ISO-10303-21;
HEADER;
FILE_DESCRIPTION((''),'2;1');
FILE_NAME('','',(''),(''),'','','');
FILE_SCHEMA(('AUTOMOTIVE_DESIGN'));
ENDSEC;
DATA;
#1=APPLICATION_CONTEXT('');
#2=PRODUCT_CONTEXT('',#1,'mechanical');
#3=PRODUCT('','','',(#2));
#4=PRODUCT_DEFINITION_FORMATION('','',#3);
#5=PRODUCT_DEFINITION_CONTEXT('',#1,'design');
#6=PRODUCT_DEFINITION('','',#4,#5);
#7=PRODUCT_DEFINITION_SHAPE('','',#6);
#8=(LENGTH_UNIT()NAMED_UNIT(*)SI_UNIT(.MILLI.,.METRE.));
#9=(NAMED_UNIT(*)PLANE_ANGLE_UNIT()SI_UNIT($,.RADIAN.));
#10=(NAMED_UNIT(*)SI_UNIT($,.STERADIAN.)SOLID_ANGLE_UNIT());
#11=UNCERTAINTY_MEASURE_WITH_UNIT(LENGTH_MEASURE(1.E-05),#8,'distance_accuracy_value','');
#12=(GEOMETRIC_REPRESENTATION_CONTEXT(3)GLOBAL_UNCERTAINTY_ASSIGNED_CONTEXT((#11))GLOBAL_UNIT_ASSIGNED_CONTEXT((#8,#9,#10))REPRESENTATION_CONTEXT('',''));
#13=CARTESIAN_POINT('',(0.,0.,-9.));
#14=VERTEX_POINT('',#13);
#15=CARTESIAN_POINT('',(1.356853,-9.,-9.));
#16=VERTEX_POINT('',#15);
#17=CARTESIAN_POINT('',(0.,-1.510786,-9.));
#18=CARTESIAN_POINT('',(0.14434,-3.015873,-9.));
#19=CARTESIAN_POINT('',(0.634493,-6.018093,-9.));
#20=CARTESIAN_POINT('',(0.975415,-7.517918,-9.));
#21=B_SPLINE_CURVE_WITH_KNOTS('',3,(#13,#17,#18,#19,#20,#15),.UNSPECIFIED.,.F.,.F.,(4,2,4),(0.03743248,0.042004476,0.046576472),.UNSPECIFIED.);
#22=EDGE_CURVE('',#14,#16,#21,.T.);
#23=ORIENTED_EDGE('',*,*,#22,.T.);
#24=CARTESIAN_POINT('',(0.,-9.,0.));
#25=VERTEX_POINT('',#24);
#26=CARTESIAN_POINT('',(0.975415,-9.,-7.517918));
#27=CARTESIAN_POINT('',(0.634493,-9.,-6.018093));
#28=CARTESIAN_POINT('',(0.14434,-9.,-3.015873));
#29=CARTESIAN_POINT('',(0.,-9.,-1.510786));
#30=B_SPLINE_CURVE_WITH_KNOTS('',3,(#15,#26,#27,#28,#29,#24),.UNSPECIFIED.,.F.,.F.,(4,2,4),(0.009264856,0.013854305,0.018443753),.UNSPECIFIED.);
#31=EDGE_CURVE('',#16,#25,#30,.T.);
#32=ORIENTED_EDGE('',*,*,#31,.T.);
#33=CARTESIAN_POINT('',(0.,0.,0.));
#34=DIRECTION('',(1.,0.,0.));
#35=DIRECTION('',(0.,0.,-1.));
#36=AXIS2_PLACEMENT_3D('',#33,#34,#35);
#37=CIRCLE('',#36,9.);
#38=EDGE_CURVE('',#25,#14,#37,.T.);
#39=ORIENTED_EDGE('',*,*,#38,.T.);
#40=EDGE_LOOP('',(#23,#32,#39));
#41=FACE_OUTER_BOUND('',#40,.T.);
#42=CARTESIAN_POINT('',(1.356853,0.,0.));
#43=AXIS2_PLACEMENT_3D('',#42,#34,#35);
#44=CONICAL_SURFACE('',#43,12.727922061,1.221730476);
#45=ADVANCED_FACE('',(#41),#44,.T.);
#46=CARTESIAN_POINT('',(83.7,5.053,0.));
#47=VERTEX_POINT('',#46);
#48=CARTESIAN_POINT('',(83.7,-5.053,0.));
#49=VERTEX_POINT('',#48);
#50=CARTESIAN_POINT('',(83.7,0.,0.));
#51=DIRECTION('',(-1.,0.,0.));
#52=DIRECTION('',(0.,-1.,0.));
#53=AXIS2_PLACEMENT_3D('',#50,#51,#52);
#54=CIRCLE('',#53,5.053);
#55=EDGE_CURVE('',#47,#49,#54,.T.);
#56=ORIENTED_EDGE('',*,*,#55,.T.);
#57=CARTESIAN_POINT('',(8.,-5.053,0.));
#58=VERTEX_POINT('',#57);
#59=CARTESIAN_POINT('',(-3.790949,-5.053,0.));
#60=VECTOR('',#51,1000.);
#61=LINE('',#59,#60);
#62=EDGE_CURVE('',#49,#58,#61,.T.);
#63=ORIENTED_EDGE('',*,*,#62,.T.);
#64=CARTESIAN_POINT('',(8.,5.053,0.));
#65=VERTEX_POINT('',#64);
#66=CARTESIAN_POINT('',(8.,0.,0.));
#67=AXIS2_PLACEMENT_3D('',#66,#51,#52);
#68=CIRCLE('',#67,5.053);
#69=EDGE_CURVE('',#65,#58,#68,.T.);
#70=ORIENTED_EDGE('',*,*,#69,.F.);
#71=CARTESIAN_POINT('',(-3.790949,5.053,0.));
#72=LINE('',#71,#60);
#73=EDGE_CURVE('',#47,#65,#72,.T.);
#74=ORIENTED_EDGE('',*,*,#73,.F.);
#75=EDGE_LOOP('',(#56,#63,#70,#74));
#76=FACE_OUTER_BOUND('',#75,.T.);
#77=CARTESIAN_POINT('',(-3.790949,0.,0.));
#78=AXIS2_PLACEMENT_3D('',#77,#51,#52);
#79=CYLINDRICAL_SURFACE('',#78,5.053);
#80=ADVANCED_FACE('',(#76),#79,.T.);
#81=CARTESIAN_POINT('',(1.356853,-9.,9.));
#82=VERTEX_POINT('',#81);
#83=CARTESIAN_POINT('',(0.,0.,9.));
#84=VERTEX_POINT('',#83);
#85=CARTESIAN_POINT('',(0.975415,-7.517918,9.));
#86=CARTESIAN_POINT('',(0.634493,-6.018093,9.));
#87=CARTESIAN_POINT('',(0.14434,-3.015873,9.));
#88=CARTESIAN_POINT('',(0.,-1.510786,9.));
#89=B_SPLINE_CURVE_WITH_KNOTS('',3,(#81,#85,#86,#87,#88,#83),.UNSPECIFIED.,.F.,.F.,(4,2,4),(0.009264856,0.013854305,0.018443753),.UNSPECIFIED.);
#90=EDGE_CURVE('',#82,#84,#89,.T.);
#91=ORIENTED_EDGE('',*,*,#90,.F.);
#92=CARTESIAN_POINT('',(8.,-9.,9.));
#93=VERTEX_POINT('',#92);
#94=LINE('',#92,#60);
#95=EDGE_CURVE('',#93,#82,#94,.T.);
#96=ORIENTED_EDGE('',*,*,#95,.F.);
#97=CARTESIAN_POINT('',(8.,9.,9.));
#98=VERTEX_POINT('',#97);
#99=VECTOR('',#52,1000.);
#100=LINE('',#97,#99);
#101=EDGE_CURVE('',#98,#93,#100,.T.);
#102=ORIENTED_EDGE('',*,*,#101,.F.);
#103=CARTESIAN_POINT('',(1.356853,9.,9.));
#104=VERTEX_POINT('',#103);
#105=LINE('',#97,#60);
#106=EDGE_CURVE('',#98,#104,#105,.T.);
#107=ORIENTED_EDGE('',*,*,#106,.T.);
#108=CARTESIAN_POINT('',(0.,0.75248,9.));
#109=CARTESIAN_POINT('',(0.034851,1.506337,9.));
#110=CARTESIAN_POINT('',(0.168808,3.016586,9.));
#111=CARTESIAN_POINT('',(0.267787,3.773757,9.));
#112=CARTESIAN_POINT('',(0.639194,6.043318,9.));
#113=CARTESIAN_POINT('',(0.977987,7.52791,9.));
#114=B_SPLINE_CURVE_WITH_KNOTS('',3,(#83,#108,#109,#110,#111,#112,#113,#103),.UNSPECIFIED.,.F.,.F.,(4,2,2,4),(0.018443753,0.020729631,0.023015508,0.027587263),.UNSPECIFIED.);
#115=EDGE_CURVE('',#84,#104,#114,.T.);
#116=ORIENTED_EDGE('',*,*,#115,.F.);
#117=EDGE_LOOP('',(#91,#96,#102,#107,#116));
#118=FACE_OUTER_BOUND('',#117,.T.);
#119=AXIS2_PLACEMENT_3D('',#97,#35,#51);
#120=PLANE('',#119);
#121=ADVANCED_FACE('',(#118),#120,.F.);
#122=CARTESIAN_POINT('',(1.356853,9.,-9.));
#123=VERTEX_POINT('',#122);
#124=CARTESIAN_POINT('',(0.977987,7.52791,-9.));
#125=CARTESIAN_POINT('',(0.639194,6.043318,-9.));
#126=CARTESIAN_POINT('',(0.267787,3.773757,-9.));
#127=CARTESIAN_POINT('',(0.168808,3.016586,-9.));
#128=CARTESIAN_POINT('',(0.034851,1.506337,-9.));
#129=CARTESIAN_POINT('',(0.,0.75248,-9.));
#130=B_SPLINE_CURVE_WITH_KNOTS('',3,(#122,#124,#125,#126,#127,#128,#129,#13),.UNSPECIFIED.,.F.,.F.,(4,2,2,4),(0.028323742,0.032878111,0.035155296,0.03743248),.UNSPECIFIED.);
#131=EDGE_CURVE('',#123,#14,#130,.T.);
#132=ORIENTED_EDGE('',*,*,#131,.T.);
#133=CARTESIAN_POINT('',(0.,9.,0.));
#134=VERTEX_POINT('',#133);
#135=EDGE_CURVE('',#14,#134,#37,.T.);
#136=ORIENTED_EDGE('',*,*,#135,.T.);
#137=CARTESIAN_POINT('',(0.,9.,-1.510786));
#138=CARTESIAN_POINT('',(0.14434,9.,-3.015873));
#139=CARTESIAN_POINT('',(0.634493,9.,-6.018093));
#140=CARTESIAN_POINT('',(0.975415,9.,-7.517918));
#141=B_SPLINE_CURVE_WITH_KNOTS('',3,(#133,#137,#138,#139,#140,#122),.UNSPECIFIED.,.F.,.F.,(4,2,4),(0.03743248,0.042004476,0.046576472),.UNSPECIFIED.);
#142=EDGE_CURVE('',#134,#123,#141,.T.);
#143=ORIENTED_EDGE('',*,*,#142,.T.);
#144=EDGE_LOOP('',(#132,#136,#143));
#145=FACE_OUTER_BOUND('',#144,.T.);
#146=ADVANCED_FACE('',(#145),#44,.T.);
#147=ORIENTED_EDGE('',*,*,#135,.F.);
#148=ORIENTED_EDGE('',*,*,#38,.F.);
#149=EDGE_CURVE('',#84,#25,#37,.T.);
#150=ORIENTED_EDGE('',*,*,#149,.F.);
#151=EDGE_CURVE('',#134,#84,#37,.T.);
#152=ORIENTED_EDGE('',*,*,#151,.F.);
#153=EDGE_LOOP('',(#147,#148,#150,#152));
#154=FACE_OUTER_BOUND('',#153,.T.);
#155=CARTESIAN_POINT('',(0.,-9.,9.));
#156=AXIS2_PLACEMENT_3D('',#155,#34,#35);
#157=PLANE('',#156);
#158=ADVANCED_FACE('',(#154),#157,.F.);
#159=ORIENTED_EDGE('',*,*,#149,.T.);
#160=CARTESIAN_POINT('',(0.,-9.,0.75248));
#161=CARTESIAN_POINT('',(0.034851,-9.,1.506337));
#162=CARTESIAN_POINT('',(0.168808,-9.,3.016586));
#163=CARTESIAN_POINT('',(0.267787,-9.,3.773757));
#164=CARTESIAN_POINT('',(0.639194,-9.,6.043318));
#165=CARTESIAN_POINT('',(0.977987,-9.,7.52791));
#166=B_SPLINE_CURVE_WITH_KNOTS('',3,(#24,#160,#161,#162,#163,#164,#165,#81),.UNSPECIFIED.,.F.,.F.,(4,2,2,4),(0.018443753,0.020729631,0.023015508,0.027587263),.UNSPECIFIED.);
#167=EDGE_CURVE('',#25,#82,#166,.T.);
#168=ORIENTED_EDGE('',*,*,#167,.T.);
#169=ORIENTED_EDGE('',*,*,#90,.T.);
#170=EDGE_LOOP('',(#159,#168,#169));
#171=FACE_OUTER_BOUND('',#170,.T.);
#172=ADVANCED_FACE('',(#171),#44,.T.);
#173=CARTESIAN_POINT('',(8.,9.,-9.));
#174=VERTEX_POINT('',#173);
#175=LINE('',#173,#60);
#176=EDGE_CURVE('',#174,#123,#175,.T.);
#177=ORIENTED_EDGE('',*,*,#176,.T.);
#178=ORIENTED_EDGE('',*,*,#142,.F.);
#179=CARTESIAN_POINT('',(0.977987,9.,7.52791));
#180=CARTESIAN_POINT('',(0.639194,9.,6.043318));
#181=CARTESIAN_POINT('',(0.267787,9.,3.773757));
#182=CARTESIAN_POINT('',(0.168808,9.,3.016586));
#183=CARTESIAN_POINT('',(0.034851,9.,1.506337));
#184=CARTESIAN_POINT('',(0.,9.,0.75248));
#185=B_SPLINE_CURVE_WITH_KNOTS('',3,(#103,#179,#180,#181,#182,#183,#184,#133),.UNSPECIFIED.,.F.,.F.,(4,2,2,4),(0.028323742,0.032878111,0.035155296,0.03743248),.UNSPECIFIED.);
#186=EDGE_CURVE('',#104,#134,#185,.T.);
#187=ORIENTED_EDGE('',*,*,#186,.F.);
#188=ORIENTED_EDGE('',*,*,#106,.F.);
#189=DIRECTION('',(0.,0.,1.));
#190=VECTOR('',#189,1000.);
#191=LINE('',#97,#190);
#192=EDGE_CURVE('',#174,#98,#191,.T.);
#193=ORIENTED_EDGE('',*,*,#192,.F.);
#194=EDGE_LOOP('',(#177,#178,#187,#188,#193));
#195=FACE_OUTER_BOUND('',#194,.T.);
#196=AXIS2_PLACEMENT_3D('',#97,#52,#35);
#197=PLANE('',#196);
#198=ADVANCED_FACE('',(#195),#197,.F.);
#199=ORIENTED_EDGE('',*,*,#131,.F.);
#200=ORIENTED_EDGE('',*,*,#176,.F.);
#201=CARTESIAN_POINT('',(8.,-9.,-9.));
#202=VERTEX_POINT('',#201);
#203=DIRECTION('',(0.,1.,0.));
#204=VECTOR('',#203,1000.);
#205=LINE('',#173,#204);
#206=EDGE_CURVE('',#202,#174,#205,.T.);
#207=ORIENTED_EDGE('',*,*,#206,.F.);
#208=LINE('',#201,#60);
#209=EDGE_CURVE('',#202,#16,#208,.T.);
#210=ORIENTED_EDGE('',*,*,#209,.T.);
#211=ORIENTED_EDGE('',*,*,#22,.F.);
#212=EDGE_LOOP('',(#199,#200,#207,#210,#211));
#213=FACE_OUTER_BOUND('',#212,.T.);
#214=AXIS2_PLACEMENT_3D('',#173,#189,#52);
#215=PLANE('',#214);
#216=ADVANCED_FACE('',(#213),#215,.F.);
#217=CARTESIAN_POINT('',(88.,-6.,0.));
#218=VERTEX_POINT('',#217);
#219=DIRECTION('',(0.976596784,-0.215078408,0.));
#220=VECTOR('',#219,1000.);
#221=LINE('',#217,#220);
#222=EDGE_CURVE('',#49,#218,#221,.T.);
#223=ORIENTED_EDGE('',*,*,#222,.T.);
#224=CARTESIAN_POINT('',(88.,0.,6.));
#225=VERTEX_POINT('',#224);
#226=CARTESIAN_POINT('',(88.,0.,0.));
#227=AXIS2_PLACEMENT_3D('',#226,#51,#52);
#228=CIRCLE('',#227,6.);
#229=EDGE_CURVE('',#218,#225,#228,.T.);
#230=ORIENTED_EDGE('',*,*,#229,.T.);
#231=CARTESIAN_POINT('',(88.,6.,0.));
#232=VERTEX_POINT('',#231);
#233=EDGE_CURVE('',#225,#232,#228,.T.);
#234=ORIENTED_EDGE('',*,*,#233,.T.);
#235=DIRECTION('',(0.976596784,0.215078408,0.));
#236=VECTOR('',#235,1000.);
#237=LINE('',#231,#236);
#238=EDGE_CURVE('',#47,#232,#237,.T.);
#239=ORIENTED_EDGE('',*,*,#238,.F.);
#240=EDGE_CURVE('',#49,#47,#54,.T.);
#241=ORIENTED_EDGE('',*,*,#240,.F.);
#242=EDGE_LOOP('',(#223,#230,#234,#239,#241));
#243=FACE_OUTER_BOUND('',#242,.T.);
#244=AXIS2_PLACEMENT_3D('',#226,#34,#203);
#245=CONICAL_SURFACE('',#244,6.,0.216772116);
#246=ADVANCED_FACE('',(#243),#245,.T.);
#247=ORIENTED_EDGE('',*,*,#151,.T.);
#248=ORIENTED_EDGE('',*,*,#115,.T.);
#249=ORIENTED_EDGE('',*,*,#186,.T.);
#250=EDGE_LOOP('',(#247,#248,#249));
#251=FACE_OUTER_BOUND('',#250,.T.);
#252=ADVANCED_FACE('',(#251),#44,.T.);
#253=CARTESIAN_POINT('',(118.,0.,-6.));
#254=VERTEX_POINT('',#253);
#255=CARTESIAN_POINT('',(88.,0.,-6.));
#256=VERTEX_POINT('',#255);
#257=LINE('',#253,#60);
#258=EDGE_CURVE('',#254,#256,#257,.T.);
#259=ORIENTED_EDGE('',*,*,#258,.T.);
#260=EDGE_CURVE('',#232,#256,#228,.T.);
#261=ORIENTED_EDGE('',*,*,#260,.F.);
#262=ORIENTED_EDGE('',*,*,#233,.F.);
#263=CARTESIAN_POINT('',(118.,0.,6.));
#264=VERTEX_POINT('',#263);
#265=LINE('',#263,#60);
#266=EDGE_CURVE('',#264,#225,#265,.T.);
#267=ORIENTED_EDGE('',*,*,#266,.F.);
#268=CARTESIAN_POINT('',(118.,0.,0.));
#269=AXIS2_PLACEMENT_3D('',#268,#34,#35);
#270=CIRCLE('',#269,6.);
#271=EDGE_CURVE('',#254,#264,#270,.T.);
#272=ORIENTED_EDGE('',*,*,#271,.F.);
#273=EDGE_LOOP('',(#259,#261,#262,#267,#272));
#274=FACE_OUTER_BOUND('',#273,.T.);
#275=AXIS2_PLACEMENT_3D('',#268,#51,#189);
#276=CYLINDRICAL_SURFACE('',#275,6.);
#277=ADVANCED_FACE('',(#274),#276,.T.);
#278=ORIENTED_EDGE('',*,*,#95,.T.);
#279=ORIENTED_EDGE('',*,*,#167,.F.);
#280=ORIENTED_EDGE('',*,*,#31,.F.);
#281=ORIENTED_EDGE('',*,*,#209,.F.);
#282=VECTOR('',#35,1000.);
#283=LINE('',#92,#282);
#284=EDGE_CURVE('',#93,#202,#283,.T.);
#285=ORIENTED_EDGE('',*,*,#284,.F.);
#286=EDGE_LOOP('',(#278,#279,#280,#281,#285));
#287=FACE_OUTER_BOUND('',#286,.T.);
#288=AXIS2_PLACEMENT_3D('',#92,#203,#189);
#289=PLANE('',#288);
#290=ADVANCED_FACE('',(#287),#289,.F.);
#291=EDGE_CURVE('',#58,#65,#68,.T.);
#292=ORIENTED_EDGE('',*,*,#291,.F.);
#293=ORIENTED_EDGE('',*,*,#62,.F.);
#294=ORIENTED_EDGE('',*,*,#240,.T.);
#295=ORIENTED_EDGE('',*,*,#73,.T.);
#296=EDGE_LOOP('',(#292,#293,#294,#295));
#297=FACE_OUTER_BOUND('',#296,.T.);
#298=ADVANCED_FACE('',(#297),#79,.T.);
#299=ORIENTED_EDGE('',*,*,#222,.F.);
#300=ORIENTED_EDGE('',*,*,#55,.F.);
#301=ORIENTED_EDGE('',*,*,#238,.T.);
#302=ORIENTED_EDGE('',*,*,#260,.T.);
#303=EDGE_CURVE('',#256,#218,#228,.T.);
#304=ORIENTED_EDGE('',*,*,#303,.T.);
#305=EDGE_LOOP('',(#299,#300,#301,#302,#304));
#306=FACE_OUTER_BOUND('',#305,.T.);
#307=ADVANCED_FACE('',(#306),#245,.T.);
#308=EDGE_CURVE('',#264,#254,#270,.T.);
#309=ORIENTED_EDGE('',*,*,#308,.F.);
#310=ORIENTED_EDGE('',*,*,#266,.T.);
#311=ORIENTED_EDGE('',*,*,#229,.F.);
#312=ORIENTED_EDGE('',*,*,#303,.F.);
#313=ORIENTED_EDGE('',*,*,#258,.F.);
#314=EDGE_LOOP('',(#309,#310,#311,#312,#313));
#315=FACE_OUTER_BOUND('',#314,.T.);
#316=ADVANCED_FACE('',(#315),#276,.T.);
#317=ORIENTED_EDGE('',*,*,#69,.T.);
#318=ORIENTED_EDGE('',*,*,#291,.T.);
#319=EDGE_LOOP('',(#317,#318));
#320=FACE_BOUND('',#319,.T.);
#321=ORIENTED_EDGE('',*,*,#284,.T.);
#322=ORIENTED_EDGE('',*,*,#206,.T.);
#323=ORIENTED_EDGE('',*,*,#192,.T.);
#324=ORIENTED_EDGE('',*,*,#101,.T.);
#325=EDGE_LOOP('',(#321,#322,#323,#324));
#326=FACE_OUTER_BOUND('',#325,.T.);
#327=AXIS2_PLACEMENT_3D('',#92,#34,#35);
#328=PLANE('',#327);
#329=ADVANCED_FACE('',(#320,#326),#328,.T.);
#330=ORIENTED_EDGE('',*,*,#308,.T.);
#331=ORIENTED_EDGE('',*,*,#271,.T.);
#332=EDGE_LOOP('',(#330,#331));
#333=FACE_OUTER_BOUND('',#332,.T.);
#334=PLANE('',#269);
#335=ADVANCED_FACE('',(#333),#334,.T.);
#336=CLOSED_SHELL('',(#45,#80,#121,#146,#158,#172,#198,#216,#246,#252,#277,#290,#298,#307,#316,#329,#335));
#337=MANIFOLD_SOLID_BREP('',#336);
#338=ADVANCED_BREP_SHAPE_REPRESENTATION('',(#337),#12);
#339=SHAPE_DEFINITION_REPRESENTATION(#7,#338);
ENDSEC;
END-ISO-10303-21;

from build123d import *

# Parameters (mm, degrees)
SKETCH1_W      = 18
SKETCH1_H      = 18
BASEHEAD_DEPTH = 8
SKETCH2_R      = 6
BASEBODY_DEPTH = 110


with BuildPart() as part:
    # Sketch1 → BaseHead (new body)
    with BuildSketch(Plane(origin=(0, 0, 0), x_dir=(0, 0, -1), z_dir=(1, 0, 0))):
        Rectangle(SKETCH1_W, SKETCH1_H)
    extrude(amount=BASEHEAD_DEPTH)

    # Sketch4 → HeadChamfer (revolve, cut)
    with BuildSketch(Plane(origin=(-7.181436497, -8, 8), x_dir=(-1, 0, 0), z_dir=(0, -0.7071067811865485, -0.7071067811865466))):
        Polygon((-7.181436497, 20.313708499), (-7.181436497, 24.04163056), (-8.538289163, 24.04163056), align=None)
    revolve(axis=Axis((8.946843605, 0, 0), (-1, 0, 0)), mode=Mode.SUBTRACT)

    # Sketch2 → BaseBody (add)
    with BuildSketch(Plane(origin=(8, 0, 0), x_dir=(0, 0, -1), z_dir=(1, 0, 0))):
        Circle(SKETCH2_R)
    extrude(amount=BASEBODY_DEPTH)

    # Sketch5 → Cut-Revolve1 (revolve, cut)
    with BuildSketch(Plane(origin=(-43.209051362, 5, 0), x_dir=(-1, 0, 0), z_dir=(0, 0, 1))):
        Polygon((-131.209051362, 11), (-51.209051362, 11), (-51.209051362, 10.053), (-126.909051362, 10.053), align=None)
    revolve(axis=Axis((-3.790948638, 0, 0), (1, 0, 0)), mode=Mode.SUBTRACT)


solid = part.part
